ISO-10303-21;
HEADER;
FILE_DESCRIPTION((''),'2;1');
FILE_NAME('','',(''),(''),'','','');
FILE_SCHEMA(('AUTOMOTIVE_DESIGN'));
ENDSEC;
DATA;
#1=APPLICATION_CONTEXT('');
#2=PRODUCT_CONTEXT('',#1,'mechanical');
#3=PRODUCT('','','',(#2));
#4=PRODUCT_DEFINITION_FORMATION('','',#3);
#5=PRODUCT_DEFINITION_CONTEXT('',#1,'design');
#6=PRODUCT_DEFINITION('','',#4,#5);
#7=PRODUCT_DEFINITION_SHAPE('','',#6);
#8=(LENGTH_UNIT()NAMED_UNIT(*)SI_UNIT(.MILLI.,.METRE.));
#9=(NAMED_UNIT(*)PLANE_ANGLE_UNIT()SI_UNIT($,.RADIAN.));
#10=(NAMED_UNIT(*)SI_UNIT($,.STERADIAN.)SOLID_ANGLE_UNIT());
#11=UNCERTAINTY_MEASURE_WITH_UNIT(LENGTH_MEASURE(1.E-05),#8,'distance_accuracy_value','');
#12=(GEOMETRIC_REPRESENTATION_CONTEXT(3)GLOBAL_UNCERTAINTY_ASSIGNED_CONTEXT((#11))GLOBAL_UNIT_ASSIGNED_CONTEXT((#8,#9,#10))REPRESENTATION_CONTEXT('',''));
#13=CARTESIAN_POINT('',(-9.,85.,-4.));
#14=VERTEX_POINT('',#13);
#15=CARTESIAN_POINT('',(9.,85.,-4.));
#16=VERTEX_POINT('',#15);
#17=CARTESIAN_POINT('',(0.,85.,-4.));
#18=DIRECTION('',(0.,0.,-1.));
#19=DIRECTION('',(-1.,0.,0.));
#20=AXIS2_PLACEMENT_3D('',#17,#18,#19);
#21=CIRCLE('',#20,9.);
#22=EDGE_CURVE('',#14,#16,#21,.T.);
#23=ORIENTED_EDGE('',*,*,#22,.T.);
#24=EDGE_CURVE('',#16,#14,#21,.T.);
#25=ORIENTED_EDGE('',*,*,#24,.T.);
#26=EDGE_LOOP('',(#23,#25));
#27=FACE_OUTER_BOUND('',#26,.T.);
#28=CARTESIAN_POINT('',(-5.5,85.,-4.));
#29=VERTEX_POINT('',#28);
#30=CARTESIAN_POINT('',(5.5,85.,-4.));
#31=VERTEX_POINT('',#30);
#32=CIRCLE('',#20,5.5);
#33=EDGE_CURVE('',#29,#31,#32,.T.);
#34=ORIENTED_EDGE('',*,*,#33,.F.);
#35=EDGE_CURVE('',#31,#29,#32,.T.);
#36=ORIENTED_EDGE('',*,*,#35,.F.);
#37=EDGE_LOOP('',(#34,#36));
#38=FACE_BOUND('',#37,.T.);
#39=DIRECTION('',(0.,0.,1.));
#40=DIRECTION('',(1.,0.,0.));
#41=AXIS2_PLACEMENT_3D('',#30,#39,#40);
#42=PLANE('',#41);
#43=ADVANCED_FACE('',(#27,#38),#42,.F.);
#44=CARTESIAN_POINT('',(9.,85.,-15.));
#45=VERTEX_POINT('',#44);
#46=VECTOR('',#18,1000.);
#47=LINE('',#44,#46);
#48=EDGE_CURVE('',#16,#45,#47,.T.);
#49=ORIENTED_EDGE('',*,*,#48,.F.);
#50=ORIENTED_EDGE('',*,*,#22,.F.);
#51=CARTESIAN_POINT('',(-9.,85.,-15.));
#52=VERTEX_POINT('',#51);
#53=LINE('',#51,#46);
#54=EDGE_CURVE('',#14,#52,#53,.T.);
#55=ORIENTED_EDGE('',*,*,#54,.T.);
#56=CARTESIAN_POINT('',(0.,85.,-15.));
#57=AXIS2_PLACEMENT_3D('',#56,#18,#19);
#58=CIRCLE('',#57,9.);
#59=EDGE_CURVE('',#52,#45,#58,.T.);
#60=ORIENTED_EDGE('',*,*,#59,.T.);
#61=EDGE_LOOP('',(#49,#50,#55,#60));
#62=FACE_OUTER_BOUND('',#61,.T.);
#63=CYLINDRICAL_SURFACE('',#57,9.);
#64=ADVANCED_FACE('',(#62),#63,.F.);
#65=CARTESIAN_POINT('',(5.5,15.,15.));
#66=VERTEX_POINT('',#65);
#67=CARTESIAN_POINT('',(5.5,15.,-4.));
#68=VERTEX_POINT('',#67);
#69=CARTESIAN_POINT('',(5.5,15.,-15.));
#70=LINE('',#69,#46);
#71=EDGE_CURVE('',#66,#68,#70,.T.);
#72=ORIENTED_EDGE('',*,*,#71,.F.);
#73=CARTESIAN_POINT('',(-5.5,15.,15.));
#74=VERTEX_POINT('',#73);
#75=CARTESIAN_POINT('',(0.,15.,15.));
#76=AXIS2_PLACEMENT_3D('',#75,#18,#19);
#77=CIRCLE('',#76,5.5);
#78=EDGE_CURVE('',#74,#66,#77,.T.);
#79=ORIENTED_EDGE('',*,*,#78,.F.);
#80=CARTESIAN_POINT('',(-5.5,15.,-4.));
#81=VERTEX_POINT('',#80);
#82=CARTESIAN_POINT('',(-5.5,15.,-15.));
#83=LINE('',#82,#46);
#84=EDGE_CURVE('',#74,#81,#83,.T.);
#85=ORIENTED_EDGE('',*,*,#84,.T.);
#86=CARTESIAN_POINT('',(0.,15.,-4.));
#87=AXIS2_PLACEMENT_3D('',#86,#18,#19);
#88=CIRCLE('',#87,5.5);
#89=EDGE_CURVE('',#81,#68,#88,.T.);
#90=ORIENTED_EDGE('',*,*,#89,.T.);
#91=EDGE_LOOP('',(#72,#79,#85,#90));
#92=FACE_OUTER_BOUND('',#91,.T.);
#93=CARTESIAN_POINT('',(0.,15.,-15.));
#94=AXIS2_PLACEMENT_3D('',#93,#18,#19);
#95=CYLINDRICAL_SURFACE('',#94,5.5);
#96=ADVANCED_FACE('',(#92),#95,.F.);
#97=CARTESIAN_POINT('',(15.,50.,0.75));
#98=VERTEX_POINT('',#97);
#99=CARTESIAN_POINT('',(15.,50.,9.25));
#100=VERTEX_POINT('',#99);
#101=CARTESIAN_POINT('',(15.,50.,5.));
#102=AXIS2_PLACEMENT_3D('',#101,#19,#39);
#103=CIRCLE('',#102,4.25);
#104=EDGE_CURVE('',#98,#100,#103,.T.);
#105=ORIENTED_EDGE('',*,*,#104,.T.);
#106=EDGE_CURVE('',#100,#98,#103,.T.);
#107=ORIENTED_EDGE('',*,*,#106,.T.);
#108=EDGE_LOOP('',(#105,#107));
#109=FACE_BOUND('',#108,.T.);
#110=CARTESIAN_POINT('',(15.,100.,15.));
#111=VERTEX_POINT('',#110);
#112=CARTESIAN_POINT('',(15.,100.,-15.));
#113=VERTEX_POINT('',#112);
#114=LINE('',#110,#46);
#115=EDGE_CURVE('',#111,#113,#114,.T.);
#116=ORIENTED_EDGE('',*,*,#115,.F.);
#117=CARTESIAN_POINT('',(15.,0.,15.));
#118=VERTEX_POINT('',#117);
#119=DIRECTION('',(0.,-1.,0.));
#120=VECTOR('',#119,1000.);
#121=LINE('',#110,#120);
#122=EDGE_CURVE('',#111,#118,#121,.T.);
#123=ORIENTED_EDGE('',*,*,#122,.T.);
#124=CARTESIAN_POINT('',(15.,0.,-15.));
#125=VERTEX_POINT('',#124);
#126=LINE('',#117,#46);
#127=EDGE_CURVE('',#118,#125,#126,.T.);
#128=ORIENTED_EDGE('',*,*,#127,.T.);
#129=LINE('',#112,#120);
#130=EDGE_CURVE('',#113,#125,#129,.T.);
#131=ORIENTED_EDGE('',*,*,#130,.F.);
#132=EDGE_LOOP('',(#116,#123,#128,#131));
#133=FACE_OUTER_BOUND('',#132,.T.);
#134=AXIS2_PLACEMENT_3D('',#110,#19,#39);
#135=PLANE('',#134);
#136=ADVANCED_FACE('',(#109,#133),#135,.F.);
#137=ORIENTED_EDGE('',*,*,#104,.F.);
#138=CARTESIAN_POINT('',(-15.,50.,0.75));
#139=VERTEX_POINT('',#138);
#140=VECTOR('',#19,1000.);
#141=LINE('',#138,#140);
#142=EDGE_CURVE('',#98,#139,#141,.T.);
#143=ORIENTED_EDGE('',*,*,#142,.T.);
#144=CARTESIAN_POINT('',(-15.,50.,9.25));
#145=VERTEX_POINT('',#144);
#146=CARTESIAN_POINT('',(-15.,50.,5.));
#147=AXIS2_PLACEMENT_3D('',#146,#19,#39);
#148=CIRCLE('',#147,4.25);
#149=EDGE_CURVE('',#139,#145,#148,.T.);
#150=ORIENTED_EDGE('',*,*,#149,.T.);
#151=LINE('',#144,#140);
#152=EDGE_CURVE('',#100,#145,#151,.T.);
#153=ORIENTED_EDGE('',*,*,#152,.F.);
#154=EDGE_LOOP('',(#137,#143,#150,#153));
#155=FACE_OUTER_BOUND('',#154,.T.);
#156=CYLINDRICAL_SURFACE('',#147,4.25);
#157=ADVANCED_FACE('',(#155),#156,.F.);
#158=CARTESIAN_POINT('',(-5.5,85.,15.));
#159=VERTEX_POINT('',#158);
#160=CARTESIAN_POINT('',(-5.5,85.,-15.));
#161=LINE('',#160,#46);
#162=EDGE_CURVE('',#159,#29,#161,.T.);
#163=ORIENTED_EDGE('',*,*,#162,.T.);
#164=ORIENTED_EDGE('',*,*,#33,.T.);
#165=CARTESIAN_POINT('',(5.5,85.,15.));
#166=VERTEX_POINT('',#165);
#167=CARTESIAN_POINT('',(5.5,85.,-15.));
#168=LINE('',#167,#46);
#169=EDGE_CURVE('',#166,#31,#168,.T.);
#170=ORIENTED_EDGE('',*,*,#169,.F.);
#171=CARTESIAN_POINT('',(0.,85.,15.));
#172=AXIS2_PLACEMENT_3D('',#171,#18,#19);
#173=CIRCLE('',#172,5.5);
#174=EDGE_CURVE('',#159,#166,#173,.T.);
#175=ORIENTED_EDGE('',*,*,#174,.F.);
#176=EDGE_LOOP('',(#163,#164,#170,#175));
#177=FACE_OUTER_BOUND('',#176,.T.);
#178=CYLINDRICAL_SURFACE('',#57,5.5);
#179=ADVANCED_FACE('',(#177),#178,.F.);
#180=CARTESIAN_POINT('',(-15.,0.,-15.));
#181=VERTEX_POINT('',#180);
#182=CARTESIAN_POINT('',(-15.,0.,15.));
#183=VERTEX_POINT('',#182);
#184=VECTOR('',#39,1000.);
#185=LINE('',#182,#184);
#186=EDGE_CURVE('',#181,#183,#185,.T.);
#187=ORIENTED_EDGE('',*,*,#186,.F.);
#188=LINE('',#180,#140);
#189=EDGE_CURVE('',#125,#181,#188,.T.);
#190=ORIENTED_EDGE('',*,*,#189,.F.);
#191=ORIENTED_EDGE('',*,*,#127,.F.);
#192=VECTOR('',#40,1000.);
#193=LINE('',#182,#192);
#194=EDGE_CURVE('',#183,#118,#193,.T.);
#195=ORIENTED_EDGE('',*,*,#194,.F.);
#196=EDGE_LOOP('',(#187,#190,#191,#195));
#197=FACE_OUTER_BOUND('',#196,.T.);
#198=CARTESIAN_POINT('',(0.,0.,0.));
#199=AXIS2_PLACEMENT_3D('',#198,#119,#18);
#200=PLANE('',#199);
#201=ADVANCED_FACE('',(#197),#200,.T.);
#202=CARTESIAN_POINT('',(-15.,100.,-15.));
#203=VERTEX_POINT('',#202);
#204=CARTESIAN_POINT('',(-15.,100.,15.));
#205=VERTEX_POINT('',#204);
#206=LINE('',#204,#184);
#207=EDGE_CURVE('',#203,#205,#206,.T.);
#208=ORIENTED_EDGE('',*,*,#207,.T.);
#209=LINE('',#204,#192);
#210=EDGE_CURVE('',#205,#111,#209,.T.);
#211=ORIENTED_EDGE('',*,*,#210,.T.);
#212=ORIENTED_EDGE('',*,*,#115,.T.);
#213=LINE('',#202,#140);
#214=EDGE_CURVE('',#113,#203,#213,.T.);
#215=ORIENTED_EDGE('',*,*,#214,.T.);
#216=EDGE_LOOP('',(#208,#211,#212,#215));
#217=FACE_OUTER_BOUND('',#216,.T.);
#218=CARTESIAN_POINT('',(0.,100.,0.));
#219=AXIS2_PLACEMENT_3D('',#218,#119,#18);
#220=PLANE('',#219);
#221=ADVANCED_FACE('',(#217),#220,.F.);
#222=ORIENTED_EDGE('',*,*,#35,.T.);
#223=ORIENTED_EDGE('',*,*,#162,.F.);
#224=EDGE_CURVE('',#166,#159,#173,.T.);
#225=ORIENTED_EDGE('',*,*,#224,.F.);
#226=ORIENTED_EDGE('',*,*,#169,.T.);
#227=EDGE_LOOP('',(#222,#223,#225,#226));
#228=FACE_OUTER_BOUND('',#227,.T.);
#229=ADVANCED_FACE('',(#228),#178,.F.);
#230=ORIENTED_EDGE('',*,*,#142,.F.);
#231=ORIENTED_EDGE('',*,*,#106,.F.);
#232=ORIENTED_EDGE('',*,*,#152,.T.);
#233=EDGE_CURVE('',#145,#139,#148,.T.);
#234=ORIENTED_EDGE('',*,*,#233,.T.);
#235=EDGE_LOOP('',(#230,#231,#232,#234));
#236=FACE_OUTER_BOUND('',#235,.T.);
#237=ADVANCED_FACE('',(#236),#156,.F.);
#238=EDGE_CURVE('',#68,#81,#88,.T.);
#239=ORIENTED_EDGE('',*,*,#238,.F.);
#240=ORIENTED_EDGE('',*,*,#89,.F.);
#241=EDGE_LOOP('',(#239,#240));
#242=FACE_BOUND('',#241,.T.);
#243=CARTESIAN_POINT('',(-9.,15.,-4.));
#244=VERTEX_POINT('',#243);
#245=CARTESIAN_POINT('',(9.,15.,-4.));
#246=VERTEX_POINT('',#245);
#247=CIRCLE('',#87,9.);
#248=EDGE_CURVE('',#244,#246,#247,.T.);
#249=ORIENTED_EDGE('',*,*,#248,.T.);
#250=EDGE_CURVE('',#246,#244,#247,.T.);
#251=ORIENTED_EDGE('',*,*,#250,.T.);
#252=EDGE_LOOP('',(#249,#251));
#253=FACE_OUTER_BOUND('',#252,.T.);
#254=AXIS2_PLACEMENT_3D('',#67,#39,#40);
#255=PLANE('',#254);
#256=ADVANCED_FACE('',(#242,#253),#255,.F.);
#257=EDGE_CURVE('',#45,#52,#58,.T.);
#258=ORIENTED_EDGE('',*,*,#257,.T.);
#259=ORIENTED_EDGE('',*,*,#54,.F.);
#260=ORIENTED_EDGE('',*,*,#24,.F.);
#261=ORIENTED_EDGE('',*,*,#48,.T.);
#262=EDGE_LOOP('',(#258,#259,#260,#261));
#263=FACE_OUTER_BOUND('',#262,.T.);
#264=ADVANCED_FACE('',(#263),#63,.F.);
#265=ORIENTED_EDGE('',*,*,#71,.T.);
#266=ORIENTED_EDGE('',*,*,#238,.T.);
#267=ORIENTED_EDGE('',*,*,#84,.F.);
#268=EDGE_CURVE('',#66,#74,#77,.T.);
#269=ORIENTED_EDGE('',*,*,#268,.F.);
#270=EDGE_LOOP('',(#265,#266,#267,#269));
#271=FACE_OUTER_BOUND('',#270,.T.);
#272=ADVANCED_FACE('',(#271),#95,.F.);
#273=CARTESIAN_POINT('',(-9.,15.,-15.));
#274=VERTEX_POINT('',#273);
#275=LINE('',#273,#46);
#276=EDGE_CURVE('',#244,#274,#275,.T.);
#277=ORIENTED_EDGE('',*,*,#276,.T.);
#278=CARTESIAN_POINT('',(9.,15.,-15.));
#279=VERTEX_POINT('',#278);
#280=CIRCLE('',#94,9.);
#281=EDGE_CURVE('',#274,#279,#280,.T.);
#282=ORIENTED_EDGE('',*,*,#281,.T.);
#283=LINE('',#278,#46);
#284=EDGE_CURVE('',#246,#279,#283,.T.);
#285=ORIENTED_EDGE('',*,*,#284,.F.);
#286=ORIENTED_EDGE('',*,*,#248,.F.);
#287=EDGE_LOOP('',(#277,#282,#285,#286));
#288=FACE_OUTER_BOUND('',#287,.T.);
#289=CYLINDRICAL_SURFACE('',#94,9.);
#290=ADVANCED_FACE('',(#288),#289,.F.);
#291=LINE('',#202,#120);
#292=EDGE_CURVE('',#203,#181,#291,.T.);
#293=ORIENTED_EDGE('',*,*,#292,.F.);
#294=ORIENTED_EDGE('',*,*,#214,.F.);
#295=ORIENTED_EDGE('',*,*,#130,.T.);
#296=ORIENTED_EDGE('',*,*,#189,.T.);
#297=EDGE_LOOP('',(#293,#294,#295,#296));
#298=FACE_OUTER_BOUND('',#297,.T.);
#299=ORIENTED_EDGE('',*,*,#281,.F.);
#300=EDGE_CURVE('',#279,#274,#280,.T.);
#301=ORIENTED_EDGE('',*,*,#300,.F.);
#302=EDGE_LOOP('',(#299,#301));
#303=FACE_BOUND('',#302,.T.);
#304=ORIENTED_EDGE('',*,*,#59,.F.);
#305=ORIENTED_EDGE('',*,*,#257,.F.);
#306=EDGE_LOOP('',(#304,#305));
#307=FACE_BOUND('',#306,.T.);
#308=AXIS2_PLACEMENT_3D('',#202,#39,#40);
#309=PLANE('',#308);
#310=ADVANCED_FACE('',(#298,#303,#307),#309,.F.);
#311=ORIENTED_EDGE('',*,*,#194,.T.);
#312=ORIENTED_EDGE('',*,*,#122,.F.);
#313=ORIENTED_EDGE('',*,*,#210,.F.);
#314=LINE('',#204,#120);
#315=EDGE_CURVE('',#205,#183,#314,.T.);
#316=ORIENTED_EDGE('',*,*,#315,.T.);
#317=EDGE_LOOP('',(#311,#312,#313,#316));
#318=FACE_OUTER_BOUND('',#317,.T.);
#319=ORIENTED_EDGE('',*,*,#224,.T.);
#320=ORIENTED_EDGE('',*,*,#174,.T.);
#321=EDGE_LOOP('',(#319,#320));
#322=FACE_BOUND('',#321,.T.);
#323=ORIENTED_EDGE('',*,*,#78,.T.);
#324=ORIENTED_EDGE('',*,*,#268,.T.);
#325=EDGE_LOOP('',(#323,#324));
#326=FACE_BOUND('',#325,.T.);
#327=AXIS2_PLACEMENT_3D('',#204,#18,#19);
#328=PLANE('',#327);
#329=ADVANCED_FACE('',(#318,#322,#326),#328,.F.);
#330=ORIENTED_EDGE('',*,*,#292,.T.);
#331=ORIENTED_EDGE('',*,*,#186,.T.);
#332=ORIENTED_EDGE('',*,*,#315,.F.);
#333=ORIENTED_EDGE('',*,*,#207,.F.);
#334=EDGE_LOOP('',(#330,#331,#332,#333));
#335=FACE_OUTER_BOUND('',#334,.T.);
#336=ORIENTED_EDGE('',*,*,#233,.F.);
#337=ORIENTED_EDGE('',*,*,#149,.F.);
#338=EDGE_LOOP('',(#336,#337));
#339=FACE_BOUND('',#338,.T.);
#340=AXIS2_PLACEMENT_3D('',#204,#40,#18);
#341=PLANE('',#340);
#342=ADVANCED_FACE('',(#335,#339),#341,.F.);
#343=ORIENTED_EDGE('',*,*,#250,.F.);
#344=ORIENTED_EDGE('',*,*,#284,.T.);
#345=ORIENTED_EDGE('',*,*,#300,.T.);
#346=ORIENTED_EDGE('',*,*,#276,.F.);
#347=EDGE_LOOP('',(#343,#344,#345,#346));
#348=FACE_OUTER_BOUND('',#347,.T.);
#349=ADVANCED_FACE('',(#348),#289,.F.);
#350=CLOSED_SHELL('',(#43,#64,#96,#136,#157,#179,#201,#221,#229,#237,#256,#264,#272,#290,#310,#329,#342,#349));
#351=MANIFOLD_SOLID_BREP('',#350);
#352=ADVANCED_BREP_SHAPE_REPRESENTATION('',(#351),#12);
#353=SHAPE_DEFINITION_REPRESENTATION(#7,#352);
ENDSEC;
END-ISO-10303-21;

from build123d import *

# Parameters (mm, degrees)
SKETCH_1_W                = 30
SKETCH_1_H                = 30
EXTRUDE_1_DEPTH           = 100
HOLE_WIZARD_1_D           = 11
HOLE_WIZARD_1_CBORE_D     = 18
HOLE_WIZARD_1_CBORE_DEPTH = 11
HOLE_WIZARD_M10_1_D       = 8.5


with BuildPart() as part:
    # 草图1 → 凸台-拉伸1 (new body)
    with BuildSketch(Plane(origin=(0, 0, 0), x_dir=(1, 0, 0), z_dir=(0, 1, 0))):
        Rectangle(SKETCH_1_W, SKETCH_1_H)
    extrude(amount=EXTRUDE_1_DEPTH)

    # 打孔尺寸(%根据)内六角圆柱头螺钉的类型1 (through all)
    with Locations(Plane(origin=(0, 0, -15), x_dir=(-1, 0, 0), z_dir=(0, 0, -1))):
        with Locations((0, 15), (0, 85)):
            CounterBoreHole(HOLE_WIZARD_1_D / 2, HOLE_WIZARD_1_CBORE_D / 2, HOLE_WIZARD_1_CBORE_DEPTH)

    # M10 螺纹孔1 (through all)
    with Locations(Plane.ZY.offset(15)):
        with Locations((5, 50)):
            Hole(HOLE_WIZARD_M10_1_D / 2)


solid = part.part
